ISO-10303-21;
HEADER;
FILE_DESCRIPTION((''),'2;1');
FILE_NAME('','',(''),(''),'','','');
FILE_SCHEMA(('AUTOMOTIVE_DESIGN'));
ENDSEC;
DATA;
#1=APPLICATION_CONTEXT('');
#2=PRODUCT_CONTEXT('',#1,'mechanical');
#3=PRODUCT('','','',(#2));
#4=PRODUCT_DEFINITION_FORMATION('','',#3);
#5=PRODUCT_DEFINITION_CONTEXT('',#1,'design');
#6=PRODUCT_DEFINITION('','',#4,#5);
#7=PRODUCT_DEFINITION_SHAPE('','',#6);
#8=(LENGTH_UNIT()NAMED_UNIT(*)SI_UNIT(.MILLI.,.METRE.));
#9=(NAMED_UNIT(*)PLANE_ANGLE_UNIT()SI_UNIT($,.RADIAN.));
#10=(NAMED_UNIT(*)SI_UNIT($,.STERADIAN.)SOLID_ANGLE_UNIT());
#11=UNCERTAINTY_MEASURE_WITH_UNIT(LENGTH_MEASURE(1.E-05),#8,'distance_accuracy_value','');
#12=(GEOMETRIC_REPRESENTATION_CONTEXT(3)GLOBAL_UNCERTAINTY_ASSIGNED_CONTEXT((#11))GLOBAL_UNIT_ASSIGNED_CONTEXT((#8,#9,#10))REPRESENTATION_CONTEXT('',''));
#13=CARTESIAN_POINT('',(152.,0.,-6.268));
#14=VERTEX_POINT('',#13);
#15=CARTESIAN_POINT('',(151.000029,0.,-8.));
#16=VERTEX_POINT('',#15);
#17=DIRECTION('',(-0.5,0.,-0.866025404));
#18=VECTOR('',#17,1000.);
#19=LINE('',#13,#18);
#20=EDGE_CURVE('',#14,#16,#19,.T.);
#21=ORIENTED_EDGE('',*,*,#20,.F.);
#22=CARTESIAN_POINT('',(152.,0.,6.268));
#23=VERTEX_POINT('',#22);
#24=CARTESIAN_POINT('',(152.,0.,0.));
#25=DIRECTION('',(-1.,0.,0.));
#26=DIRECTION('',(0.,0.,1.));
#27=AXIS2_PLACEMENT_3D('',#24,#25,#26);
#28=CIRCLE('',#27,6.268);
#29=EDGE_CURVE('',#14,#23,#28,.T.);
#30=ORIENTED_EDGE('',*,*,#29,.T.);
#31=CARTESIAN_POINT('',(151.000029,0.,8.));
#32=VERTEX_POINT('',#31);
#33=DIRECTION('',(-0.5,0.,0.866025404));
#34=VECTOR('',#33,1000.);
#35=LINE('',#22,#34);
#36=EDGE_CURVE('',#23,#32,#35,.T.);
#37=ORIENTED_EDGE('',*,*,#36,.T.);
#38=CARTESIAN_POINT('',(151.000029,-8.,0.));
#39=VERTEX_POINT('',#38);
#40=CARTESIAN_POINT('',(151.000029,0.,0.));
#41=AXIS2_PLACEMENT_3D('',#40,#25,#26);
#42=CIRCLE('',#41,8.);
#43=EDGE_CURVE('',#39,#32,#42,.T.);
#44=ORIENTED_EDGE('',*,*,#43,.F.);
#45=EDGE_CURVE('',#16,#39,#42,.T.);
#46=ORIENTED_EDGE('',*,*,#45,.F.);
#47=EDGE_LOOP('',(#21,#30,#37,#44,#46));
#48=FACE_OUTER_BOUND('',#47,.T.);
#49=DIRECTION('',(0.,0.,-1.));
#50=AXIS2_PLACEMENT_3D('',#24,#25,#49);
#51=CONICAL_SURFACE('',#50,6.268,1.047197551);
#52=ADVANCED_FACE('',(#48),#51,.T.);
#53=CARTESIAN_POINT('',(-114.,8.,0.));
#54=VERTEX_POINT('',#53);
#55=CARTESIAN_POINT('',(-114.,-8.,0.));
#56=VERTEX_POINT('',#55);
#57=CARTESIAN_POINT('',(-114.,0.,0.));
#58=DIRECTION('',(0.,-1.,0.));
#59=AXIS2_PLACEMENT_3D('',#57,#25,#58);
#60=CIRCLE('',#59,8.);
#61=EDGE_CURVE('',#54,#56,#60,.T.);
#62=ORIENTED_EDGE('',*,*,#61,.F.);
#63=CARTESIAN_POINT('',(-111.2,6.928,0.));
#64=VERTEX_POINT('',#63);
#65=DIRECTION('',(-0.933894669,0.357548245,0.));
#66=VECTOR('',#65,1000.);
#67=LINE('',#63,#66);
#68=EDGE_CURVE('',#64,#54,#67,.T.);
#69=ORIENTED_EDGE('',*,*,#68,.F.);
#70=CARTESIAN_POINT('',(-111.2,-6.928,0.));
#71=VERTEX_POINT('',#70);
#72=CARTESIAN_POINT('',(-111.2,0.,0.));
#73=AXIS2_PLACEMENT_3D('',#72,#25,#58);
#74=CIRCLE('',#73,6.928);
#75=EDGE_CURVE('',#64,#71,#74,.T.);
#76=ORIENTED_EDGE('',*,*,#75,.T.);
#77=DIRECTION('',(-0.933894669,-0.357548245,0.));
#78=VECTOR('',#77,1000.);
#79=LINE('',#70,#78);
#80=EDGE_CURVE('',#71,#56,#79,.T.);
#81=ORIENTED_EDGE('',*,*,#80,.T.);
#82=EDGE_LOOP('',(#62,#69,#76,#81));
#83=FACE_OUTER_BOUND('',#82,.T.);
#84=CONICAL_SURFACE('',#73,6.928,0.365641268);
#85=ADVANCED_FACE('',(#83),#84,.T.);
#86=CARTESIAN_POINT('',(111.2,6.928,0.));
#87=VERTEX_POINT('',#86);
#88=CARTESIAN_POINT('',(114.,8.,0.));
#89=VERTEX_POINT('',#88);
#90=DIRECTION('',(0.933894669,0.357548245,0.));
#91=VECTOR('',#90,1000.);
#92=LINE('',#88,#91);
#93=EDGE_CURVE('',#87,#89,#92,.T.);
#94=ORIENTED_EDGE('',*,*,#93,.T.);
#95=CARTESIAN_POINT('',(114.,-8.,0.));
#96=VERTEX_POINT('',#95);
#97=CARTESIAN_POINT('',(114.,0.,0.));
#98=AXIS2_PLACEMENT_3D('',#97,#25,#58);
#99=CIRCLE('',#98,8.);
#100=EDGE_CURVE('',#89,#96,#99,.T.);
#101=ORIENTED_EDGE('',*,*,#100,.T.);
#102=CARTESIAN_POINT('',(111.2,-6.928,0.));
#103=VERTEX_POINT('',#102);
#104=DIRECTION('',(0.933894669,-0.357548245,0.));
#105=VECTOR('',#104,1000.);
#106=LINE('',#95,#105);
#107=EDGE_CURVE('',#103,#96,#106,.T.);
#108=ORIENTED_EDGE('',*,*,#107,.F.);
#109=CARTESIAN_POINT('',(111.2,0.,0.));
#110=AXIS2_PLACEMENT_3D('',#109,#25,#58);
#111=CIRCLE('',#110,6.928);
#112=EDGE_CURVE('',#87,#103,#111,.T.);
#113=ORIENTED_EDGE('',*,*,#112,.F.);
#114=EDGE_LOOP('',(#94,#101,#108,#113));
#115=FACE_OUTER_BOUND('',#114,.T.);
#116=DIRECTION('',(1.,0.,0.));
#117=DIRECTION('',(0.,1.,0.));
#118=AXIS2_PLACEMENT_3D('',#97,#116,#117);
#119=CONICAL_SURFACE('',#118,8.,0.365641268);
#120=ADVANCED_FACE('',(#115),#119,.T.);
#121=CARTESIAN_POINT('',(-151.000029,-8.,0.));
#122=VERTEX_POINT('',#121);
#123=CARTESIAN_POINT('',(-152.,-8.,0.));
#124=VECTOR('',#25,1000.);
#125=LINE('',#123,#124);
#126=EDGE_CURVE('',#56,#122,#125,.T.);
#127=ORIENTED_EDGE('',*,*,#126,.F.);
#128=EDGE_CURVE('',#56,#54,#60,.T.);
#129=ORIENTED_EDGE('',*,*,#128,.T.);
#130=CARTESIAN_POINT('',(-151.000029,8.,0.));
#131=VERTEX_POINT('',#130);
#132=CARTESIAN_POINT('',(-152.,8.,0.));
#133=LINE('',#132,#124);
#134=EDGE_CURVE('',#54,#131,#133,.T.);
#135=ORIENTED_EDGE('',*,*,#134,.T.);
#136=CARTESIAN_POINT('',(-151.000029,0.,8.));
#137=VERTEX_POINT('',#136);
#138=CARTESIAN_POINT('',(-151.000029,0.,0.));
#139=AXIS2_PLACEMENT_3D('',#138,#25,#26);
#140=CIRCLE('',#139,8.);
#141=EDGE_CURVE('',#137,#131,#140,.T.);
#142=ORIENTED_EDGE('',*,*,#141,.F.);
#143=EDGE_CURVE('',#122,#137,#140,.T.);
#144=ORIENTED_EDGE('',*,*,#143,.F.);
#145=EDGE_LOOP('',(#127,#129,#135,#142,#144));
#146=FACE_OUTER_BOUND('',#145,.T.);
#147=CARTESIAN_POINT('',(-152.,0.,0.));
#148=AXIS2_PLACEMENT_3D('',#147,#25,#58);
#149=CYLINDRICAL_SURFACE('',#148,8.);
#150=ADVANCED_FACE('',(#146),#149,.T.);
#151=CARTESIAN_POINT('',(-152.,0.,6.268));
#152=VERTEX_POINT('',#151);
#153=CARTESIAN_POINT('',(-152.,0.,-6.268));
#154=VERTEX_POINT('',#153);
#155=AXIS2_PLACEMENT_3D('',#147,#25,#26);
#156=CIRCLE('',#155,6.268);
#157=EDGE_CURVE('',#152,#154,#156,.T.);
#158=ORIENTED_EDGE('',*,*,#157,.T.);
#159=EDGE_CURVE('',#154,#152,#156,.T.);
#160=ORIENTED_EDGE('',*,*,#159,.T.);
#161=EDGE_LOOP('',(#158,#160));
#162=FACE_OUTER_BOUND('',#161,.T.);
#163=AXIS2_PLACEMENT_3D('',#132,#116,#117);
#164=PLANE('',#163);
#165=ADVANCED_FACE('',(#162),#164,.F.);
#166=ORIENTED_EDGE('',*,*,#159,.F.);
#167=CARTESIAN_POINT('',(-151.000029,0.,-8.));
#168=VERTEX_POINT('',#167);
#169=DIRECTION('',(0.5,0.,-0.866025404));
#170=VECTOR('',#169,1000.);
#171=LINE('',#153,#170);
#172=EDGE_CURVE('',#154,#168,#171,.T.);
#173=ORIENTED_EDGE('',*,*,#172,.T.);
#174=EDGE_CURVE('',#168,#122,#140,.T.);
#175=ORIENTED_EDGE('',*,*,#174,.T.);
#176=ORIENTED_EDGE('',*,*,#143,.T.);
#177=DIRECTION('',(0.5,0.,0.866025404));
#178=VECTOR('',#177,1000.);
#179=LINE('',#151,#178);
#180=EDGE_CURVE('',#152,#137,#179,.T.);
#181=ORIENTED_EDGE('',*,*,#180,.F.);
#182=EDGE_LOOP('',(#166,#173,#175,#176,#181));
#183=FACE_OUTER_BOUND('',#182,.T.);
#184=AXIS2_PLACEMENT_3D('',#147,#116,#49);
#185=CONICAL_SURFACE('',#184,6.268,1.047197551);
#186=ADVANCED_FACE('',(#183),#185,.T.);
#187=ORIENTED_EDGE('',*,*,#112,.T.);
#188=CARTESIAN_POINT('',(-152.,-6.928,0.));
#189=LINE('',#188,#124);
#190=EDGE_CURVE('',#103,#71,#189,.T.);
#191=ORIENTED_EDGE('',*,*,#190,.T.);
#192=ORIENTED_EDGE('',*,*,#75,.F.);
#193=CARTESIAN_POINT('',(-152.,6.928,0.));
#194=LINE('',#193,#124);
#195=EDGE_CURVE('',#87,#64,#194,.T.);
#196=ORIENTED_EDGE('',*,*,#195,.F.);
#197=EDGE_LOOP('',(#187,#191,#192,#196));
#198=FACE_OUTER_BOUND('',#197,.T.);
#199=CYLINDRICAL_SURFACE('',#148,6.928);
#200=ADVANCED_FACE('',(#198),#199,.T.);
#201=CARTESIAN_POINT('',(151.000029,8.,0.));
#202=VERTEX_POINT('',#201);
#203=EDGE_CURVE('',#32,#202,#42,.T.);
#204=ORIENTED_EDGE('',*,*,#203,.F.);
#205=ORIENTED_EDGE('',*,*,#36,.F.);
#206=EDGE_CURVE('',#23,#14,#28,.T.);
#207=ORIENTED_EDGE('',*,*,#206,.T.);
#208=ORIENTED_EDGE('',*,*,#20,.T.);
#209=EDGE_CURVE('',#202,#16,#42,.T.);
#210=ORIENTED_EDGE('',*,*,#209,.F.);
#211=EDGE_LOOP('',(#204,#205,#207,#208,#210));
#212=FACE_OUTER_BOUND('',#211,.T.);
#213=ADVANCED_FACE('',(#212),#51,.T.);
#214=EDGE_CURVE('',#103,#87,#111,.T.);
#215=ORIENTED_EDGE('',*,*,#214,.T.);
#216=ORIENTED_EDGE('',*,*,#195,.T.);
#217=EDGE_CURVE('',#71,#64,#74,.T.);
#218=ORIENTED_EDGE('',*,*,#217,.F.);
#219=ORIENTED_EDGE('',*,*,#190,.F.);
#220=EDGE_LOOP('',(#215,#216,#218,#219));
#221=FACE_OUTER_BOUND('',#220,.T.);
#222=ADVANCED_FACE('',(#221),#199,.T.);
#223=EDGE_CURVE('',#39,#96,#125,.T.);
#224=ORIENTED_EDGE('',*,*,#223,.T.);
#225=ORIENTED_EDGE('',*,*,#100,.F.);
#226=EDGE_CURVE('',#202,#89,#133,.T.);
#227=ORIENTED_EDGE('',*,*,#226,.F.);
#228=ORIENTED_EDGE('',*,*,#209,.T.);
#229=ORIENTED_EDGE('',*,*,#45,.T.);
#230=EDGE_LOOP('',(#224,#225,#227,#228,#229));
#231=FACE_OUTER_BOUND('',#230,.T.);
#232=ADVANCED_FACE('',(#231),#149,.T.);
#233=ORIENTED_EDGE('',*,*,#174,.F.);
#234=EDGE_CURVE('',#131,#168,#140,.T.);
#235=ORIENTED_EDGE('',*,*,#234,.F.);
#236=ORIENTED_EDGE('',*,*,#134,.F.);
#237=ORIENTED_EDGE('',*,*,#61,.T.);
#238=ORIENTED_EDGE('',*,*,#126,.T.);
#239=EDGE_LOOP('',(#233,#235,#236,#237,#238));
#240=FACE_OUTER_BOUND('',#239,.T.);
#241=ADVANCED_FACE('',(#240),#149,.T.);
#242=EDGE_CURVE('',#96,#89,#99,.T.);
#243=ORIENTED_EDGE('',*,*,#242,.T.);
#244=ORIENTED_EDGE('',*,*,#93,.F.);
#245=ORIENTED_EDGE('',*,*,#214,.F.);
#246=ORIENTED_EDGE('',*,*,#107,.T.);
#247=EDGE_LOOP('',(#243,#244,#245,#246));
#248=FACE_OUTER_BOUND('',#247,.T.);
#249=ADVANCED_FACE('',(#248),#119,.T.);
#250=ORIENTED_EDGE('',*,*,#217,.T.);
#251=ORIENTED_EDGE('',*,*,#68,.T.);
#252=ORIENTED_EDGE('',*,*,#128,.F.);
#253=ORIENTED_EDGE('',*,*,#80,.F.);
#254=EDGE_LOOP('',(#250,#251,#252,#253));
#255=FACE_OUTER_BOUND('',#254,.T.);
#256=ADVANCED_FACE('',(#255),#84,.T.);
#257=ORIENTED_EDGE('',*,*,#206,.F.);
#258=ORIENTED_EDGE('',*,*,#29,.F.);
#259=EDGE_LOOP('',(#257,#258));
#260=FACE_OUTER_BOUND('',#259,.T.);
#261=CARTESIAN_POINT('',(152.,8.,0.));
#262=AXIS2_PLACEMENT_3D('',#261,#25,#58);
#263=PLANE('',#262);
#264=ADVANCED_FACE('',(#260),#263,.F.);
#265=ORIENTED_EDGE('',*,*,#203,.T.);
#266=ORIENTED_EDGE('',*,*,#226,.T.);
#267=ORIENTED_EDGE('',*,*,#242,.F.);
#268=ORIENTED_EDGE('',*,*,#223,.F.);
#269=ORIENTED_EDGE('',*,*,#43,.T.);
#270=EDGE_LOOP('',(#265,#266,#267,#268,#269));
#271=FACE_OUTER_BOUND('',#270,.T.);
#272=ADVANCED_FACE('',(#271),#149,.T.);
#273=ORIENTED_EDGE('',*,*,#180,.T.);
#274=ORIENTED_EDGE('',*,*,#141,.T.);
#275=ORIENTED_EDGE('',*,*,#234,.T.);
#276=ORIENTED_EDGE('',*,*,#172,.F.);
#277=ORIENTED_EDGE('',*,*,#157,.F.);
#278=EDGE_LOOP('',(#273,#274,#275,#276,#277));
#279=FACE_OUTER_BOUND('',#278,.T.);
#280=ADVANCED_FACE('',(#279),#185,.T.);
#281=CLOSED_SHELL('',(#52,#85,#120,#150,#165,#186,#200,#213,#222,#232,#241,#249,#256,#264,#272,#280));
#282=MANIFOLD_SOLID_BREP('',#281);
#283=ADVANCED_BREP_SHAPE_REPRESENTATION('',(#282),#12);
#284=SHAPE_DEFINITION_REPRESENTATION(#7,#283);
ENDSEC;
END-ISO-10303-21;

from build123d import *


with BuildPart() as part:
    # 草图1 → Revolve 558 (revolve)
    with BuildSketch(Plane.XY, mode=Mode.PRIVATE) as revolve_558_sk:
        Polygon((-152, 8), (-114, 8), (-111.2, 6.928), (111.2, 6.928), (114, 8), (152, 8), (152, 0), (-152, 0), align=None)
    revolve(revolve_558_sk.sketch.rotate(Axis((-152, 0, 0), (1, 0, 0)), 180), axis=Axis((-152, 0, 0), (1, 0, 0)))

    # 草图2 → Cut-Revolve 607 (revolve, cut)
    with BuildSketch(Plane.XY, mode=Mode.PRIVATE) as cut_revolve_607_sk:
        Polygon((-152.999970666, 8), (-151.000029334, 8), (-152, 6.268), align=None)
    cut_revolve_607 = revolve(cut_revolve_607_sk.sketch.rotate(Axis((-26.952426469, 0, 0), (1, 0, 0)), 180), axis=Axis((-26.952426469, 0, 0), (1, 0, 0)), mode=Mode.SUBTRACT)

    # 镜向1: Cut-Revolve 607 across plane
    add(cut_revolve_607.mirror(Plane(origin=(0, 0, 0), x_dir=(0, 0, 1), z_dir=(1, 0, 0))), mode=Mode.SUBTRACT)


solid = part.part
